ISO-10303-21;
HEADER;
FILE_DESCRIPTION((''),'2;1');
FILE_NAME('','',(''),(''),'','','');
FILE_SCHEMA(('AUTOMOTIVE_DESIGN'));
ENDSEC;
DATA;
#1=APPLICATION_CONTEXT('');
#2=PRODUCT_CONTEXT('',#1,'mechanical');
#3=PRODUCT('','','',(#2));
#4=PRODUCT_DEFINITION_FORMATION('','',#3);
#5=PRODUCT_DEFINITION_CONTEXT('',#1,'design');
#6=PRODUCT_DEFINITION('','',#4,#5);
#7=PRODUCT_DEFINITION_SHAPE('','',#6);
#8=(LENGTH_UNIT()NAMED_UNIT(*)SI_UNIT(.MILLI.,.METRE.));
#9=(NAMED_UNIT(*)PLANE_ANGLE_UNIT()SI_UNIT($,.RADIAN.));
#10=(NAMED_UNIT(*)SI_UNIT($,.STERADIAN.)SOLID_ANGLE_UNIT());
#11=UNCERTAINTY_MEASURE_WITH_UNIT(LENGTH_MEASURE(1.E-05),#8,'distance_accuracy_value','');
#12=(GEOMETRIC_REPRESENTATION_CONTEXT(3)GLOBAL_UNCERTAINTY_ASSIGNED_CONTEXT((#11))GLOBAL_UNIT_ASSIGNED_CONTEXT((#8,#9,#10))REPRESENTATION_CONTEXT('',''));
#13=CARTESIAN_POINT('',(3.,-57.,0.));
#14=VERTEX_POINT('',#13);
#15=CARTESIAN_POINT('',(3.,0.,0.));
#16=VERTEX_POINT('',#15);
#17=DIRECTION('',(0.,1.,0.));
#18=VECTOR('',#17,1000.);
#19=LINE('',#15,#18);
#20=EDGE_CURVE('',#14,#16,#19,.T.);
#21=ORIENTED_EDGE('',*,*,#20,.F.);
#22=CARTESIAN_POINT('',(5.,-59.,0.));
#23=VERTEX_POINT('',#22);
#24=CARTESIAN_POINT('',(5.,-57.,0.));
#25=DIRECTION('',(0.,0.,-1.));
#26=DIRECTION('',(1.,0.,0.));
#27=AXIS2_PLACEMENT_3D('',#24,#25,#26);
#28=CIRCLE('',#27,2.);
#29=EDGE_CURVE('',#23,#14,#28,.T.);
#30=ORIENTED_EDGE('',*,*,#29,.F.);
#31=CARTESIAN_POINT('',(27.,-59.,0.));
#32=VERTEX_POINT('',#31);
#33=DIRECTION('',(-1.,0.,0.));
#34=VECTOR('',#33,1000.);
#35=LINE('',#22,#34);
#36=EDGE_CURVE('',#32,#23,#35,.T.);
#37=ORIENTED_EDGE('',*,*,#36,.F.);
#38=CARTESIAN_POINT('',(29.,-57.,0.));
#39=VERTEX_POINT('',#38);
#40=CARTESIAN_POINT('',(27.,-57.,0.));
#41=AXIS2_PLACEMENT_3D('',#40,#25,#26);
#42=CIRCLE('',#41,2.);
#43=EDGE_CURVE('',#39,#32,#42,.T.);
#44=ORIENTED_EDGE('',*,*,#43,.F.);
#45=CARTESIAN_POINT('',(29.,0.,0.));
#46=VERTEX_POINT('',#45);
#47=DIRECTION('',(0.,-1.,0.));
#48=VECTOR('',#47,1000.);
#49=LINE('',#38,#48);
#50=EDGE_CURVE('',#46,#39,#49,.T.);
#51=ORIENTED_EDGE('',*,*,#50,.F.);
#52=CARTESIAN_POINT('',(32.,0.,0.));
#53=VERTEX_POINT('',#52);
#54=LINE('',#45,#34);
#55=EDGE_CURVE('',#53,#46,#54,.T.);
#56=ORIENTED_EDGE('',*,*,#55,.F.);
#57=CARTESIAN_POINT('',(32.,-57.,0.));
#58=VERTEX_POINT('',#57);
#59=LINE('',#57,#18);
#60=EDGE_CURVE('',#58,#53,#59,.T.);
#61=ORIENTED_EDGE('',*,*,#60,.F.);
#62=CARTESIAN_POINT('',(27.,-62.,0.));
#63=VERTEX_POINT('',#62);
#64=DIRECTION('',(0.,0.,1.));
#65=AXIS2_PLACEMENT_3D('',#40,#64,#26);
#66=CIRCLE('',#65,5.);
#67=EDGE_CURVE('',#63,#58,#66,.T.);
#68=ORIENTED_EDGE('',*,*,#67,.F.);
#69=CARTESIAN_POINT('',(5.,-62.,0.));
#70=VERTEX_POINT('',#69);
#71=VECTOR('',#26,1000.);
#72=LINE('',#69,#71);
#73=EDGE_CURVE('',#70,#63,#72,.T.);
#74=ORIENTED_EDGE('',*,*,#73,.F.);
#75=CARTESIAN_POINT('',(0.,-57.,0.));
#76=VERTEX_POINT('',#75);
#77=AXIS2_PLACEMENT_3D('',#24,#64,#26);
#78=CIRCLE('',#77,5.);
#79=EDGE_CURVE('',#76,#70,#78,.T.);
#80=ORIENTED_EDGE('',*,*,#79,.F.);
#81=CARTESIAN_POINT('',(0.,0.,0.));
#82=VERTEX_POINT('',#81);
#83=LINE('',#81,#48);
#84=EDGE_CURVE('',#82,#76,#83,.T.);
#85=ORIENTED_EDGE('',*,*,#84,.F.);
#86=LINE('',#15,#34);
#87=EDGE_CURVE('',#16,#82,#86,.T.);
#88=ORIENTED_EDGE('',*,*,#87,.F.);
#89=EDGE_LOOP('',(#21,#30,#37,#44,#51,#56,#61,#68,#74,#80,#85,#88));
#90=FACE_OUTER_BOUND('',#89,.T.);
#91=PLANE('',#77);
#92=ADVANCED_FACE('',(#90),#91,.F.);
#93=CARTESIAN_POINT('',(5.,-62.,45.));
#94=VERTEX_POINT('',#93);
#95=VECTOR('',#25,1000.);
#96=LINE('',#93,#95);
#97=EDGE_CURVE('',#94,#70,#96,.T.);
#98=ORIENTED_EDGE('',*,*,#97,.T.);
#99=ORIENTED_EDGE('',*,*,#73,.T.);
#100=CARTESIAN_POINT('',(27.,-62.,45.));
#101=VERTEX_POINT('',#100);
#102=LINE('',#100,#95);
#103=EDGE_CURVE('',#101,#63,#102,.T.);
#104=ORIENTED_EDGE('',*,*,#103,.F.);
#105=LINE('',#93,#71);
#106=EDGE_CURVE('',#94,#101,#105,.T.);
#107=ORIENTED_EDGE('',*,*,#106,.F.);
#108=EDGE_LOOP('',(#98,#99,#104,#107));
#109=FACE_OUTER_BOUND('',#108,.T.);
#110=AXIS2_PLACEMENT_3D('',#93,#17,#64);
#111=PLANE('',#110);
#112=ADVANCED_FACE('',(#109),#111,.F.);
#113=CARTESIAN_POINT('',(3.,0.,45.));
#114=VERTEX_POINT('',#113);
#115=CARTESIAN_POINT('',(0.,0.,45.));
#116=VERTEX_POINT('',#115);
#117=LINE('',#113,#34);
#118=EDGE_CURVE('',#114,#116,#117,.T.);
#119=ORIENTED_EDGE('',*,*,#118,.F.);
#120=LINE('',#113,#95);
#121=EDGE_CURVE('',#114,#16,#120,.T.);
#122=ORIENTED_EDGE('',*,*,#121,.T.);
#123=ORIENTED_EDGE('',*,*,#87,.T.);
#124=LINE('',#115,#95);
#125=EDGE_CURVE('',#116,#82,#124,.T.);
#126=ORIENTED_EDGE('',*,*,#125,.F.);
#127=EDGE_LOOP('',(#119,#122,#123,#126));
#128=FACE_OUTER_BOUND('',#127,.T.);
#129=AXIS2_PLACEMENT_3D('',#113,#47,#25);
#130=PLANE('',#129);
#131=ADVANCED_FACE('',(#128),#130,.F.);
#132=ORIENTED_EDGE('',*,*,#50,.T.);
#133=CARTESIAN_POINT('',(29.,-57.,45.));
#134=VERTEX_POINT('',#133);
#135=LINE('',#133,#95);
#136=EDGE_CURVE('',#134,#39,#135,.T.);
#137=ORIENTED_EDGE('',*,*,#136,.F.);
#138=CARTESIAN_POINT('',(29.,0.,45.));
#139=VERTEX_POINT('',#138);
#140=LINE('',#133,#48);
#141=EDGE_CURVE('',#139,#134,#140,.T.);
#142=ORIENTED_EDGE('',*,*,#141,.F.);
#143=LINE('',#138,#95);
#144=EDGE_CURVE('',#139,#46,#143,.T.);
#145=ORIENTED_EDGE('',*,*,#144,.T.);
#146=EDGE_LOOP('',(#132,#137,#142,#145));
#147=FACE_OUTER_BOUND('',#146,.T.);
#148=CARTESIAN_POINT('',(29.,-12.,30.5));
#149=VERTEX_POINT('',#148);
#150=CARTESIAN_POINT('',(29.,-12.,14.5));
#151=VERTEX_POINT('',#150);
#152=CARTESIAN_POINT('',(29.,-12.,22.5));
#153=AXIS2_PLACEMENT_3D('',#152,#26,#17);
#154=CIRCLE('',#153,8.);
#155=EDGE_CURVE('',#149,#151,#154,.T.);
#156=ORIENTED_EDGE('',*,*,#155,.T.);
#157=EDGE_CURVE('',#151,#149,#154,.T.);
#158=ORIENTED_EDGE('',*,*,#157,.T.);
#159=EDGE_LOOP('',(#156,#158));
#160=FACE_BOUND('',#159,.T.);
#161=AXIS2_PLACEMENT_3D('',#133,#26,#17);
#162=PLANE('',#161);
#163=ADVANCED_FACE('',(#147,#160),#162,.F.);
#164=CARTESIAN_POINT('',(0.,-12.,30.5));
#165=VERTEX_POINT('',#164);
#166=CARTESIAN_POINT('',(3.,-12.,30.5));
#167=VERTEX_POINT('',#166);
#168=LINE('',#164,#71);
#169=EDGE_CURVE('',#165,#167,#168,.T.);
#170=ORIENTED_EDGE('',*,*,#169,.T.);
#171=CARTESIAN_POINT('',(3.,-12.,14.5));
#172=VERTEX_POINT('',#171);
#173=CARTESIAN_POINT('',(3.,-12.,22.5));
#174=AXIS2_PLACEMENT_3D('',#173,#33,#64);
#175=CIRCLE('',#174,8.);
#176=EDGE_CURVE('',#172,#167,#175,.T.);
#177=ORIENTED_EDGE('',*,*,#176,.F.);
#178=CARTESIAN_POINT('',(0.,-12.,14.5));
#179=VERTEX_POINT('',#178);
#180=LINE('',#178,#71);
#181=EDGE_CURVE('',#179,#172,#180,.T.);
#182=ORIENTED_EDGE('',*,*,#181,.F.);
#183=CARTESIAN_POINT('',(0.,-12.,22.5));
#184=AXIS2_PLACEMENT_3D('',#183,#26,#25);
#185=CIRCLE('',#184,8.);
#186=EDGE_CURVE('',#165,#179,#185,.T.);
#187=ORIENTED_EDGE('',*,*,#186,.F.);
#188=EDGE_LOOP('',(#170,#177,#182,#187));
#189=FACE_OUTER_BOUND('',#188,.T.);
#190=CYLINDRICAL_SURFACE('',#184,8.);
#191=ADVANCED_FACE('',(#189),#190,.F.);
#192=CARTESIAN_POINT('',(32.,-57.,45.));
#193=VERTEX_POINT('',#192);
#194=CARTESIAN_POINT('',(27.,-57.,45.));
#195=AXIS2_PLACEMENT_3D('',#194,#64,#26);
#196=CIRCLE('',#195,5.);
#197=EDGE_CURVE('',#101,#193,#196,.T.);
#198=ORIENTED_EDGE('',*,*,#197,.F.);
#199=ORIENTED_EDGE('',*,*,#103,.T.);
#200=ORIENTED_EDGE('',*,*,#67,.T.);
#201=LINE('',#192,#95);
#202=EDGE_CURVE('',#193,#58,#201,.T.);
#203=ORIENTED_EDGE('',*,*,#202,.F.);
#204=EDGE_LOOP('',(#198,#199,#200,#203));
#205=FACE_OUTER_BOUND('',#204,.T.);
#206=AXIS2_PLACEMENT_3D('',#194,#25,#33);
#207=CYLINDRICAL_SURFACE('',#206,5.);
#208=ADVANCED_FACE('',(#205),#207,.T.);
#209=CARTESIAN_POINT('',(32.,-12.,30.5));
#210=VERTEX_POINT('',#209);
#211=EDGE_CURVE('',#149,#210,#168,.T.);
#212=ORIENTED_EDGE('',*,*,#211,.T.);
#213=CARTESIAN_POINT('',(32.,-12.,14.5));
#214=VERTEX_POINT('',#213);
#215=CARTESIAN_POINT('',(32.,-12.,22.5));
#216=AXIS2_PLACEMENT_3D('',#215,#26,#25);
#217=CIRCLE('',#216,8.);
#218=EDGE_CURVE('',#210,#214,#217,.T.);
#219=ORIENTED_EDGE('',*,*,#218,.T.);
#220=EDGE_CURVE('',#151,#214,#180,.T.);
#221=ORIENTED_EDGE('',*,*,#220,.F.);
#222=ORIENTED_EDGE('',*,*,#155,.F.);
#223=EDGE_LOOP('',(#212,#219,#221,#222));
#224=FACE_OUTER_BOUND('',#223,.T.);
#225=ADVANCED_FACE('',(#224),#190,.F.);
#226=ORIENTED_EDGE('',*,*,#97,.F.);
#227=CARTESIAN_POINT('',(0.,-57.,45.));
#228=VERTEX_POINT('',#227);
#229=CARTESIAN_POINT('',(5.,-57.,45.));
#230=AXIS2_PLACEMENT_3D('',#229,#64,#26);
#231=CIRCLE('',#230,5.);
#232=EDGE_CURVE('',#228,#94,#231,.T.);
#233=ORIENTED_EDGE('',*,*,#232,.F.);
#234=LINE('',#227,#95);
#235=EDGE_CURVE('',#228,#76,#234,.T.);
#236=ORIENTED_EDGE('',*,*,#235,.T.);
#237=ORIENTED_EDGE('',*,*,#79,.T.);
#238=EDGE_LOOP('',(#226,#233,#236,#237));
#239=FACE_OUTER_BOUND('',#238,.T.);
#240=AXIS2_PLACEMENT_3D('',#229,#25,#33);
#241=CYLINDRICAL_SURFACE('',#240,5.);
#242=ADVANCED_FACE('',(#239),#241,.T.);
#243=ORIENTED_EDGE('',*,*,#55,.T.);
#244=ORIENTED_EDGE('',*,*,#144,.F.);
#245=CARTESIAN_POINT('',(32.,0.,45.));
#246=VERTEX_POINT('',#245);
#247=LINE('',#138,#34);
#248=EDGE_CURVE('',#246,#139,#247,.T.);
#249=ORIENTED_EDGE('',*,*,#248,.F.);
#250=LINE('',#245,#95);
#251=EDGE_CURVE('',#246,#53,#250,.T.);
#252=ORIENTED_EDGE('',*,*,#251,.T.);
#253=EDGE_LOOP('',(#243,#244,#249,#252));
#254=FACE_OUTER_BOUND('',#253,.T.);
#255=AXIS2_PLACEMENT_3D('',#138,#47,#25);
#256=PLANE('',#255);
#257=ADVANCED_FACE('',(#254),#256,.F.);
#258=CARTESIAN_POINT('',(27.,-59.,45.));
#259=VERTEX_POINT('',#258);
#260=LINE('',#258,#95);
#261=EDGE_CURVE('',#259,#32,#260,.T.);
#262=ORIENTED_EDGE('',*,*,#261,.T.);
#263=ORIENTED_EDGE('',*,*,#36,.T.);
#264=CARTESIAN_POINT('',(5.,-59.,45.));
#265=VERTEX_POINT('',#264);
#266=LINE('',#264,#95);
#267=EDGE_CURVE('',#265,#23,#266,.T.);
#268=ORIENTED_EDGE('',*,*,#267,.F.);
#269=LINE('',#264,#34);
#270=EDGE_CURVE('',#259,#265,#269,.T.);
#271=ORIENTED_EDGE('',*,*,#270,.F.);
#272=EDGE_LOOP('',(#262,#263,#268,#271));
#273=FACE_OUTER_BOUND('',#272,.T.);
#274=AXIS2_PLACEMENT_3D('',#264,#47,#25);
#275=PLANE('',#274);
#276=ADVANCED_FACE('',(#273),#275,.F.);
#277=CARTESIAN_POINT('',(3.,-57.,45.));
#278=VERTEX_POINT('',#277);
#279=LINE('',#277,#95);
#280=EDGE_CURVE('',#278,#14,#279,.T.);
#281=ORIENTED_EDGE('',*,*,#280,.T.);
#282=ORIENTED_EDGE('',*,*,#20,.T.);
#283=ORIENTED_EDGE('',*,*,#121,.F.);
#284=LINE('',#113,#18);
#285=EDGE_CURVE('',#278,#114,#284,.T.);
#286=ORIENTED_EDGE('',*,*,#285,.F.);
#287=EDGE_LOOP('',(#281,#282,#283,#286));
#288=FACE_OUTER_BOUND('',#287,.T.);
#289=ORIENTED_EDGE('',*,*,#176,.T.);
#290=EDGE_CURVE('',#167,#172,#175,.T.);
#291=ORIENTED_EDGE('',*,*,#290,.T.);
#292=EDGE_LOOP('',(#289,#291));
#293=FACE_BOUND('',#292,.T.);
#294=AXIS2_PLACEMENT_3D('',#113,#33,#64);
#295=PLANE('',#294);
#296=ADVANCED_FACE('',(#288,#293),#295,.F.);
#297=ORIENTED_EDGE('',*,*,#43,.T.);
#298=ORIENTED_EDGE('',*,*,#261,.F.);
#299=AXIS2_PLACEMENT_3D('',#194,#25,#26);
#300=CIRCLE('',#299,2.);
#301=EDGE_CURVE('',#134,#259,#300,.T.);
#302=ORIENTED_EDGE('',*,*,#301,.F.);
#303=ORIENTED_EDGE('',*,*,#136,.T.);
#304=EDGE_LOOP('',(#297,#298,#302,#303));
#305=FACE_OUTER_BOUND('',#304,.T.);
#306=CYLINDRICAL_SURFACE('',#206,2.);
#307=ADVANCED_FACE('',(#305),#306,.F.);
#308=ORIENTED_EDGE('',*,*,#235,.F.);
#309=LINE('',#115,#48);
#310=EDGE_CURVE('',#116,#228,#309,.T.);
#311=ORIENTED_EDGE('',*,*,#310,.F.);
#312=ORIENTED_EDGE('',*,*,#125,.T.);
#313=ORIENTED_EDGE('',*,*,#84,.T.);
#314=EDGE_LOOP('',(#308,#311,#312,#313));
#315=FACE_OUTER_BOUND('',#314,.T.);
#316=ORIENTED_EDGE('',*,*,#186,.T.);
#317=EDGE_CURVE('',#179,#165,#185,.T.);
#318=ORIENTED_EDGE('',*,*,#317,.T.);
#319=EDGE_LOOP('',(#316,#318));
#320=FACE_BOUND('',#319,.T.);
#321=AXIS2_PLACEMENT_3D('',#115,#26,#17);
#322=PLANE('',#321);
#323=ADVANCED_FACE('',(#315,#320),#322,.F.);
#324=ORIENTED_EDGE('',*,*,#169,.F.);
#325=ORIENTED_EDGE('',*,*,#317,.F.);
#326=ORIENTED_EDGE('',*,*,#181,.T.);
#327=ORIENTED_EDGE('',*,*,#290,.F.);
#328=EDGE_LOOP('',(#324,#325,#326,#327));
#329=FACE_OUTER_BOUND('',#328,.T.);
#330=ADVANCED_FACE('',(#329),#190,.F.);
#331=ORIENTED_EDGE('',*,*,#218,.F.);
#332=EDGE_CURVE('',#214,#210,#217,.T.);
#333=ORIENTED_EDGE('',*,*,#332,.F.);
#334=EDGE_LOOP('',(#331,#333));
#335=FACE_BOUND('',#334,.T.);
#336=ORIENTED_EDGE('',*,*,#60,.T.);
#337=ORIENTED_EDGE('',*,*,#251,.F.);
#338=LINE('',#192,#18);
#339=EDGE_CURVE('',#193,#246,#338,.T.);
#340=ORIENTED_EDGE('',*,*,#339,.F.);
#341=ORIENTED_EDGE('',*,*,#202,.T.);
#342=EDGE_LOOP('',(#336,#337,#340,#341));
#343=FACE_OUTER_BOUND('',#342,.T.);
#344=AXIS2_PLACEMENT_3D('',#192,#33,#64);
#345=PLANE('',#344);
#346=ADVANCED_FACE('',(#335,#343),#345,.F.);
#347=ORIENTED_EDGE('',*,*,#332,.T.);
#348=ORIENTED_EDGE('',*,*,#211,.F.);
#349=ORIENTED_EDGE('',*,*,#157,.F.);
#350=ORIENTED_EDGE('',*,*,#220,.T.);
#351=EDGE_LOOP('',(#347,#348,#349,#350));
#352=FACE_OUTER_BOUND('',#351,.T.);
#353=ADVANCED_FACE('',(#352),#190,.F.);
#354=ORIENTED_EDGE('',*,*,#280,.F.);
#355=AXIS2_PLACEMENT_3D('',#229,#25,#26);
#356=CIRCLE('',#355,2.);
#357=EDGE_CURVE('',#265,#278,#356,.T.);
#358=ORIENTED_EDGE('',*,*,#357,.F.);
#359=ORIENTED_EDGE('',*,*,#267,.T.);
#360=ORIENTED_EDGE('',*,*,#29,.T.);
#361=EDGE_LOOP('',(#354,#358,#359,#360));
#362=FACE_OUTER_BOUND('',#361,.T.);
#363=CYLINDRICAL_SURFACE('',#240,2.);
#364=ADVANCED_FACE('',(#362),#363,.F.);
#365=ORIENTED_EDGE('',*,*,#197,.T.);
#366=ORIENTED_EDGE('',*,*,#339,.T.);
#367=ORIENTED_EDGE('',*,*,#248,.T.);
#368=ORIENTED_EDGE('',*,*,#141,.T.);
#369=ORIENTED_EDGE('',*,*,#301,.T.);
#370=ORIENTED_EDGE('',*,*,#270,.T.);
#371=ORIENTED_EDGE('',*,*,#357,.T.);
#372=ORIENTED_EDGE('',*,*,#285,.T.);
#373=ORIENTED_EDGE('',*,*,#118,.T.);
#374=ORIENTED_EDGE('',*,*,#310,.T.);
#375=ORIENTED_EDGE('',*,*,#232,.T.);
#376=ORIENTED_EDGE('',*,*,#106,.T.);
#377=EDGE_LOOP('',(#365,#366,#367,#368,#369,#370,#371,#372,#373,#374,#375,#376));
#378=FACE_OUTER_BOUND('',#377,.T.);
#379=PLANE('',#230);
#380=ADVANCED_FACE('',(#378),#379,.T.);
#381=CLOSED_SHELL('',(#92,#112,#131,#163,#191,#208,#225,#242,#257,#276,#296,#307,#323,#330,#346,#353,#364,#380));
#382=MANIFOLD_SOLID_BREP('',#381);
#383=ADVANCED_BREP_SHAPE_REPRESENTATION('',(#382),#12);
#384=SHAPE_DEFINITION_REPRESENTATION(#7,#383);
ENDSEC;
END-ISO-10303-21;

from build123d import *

# Parameters (mm, degrees)
BOSS_EXTRUDE1_DEPTH = 45
SKETCH2_R           = 8
CUT_EXTRUDE1_DEPTH  = 84.024092889


with BuildPart() as part:
    # Sketch1 → Boss-Extrude1 (new body)
    with BuildSketch(Plane.XY):
        with BuildLine():
            Line((0, 0), (0, -57))
            ThreePointArc((0, -57), (1.464466094, -60.535533906), (5, -62))
            Line((5, -62), (27, -62))
            ThreePointArc((27, -62), (30.535533906, -60.535533906), (32, -57))
            Line((32, -57), (32, 0))
            Line((32, 0), (29, 0))
            Line((29, 0), (29, -57))
            ThreePointArc((29, -57), (28.414213562, -58.414213562), (27, -59))
            Line((27, -59), (5, -59))
            ThreePointArc((5, -59), (3.585786438, -58.414213562), (3, -57))
            Line((3, -57), (3, 0))
            Line((3, 0), (0, 0))
        make_face()
    extrude(amount=BOSS_EXTRUDE1_DEPTH)

    # Sketch2 → Cut-Extrude1 (cut, through all)
    with BuildSketch(Plane(origin=(32, 0, 0), x_dir=(0, 0, -1), z_dir=(1, 0, 0))):
        with Locations((-22.5, -12)):
            Circle(SKETCH2_R)
    extrude(amount=-CUT_EXTRUDE1_DEPTH, mode=Mode.SUBTRACT)


solid = part.part
